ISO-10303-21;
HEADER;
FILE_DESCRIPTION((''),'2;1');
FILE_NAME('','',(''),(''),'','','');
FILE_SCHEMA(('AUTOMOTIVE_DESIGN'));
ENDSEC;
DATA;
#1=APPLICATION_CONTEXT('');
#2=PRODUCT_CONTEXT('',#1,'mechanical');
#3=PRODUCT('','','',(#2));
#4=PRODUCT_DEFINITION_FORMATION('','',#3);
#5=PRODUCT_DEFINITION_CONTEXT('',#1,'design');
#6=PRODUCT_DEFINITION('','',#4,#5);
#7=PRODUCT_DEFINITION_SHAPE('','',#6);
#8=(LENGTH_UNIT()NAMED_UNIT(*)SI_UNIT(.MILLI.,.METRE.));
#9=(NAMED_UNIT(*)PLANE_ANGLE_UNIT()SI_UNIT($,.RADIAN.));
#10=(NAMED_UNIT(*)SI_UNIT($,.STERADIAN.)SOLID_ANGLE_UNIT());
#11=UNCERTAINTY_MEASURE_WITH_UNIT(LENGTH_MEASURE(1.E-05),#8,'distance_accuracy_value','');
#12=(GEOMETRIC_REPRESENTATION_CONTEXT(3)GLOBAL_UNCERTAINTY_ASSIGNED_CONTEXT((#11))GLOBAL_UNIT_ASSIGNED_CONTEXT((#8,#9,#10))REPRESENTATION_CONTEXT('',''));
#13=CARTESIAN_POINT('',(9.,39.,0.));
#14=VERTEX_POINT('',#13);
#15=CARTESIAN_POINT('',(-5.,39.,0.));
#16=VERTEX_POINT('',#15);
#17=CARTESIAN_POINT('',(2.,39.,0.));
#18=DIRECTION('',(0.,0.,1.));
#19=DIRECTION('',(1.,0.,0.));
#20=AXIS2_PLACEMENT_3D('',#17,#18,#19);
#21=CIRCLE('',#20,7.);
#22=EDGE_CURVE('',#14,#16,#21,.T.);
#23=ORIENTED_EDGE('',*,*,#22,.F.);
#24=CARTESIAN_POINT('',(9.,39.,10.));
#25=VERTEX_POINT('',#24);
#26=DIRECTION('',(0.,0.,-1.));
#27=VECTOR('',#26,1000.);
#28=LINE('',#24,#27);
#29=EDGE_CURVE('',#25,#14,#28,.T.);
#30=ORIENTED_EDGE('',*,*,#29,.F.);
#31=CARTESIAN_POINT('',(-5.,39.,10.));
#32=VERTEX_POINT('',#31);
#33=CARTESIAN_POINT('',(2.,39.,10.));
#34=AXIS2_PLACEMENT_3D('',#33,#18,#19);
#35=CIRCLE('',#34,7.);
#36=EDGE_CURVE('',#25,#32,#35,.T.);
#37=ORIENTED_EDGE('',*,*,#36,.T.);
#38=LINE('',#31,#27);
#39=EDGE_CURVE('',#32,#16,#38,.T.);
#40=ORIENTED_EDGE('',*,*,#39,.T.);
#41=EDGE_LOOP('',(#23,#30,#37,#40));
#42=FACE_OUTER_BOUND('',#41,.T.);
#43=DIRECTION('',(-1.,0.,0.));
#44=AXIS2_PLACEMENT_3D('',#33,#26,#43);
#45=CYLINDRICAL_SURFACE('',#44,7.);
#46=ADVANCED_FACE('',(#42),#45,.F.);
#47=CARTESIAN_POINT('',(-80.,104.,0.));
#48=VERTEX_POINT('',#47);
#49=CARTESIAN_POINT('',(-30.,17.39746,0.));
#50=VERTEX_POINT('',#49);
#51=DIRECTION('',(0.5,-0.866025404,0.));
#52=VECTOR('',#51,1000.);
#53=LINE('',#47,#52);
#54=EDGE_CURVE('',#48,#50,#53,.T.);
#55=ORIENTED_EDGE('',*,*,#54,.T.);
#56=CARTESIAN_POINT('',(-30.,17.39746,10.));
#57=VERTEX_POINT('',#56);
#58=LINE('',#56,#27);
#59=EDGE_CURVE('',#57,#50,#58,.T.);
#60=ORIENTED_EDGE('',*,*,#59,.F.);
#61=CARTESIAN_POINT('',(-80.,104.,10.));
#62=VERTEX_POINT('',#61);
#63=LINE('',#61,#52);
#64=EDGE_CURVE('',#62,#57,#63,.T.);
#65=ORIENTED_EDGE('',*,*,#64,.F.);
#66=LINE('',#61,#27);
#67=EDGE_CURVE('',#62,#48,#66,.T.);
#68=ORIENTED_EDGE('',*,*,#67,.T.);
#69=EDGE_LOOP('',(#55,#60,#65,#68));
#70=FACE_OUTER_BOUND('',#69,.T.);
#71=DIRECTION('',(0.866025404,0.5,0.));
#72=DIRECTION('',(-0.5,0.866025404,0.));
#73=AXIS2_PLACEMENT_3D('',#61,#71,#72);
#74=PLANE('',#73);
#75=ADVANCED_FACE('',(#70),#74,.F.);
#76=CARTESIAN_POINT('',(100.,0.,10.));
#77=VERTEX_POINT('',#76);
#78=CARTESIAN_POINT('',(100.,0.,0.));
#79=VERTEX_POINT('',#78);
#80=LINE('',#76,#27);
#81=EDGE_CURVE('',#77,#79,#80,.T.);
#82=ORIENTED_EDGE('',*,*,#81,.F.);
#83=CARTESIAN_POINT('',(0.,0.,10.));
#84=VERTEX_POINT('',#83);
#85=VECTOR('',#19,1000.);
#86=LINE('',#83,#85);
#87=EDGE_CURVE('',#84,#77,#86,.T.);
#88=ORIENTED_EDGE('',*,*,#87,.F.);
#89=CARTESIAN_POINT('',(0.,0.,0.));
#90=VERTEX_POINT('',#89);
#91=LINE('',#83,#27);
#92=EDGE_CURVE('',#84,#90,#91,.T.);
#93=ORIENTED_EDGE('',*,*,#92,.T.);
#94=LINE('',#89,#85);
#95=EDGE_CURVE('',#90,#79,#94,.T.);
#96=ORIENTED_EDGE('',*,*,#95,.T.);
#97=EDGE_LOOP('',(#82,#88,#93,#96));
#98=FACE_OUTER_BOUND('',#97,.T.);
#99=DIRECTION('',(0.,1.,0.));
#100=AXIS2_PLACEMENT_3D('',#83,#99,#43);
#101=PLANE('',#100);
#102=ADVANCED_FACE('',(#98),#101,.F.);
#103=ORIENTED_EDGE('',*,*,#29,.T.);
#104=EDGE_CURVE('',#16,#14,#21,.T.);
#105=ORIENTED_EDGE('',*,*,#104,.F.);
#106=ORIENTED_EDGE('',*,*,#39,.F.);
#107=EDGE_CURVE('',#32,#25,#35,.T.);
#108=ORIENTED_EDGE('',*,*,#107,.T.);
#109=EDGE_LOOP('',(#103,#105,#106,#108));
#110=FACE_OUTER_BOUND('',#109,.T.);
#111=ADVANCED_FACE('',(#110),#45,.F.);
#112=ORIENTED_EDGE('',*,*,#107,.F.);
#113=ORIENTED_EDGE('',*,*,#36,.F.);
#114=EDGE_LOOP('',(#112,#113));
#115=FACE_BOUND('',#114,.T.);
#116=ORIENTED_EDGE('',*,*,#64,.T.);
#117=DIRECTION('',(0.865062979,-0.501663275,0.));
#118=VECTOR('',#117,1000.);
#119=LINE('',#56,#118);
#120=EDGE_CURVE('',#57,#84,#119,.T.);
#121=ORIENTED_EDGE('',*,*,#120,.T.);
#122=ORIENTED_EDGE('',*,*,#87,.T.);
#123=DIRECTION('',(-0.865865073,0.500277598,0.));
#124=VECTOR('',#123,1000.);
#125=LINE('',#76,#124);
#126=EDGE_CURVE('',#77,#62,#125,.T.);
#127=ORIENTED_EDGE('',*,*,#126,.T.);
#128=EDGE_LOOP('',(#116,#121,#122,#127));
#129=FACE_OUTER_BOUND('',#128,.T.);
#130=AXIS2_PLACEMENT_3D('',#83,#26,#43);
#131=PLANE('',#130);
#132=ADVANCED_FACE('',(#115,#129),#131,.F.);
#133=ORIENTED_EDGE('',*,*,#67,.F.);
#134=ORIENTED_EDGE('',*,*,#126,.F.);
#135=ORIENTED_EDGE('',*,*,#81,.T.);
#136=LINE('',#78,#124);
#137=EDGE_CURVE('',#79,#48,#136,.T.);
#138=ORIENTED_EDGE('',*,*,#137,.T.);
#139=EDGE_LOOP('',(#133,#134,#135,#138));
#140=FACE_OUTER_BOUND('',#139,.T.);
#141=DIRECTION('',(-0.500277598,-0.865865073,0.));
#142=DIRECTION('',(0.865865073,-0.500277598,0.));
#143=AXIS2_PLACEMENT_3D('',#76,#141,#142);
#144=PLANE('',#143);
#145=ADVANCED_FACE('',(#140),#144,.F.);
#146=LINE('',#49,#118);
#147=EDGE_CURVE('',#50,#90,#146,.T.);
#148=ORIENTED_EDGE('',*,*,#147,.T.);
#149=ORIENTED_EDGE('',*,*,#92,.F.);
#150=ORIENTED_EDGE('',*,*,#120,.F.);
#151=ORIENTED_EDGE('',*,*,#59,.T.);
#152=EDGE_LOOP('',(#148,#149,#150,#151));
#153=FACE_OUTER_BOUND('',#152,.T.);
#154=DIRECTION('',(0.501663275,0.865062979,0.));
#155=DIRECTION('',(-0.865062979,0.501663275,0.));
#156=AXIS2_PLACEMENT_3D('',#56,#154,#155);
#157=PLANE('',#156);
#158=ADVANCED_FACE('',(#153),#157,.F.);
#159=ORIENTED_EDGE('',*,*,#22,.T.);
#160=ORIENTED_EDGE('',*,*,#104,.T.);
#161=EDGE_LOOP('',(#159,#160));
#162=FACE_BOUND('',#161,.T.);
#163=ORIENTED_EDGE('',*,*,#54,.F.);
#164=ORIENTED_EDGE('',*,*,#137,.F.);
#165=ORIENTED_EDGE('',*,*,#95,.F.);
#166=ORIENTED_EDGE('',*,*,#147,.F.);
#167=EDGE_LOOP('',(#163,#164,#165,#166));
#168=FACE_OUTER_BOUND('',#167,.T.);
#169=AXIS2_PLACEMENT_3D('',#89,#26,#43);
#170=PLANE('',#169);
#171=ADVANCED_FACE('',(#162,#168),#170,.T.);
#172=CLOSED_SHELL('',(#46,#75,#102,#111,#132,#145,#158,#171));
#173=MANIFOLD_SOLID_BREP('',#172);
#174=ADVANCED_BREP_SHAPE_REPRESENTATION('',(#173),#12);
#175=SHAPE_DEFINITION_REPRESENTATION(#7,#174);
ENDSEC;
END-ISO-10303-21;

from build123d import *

# Parameters (mm, degrees)
SKETCH1_R           = 7
BOSS_EXTRUDE1_DEPTH = 10


with BuildPart() as part:
    # Sketch1 → Boss-Extrude1 (new body)
    with BuildSketch(Plane.XY):
        Polygon((-80, 104), (-30, 17.397459622), (0, 0), (100, 0), align=None)
        with Locations((2, 39)):
            Circle(SKETCH1_R, mode=Mode.SUBTRACT)
    extrude(amount=BOSS_EXTRUDE1_DEPTH)


solid = part.part
